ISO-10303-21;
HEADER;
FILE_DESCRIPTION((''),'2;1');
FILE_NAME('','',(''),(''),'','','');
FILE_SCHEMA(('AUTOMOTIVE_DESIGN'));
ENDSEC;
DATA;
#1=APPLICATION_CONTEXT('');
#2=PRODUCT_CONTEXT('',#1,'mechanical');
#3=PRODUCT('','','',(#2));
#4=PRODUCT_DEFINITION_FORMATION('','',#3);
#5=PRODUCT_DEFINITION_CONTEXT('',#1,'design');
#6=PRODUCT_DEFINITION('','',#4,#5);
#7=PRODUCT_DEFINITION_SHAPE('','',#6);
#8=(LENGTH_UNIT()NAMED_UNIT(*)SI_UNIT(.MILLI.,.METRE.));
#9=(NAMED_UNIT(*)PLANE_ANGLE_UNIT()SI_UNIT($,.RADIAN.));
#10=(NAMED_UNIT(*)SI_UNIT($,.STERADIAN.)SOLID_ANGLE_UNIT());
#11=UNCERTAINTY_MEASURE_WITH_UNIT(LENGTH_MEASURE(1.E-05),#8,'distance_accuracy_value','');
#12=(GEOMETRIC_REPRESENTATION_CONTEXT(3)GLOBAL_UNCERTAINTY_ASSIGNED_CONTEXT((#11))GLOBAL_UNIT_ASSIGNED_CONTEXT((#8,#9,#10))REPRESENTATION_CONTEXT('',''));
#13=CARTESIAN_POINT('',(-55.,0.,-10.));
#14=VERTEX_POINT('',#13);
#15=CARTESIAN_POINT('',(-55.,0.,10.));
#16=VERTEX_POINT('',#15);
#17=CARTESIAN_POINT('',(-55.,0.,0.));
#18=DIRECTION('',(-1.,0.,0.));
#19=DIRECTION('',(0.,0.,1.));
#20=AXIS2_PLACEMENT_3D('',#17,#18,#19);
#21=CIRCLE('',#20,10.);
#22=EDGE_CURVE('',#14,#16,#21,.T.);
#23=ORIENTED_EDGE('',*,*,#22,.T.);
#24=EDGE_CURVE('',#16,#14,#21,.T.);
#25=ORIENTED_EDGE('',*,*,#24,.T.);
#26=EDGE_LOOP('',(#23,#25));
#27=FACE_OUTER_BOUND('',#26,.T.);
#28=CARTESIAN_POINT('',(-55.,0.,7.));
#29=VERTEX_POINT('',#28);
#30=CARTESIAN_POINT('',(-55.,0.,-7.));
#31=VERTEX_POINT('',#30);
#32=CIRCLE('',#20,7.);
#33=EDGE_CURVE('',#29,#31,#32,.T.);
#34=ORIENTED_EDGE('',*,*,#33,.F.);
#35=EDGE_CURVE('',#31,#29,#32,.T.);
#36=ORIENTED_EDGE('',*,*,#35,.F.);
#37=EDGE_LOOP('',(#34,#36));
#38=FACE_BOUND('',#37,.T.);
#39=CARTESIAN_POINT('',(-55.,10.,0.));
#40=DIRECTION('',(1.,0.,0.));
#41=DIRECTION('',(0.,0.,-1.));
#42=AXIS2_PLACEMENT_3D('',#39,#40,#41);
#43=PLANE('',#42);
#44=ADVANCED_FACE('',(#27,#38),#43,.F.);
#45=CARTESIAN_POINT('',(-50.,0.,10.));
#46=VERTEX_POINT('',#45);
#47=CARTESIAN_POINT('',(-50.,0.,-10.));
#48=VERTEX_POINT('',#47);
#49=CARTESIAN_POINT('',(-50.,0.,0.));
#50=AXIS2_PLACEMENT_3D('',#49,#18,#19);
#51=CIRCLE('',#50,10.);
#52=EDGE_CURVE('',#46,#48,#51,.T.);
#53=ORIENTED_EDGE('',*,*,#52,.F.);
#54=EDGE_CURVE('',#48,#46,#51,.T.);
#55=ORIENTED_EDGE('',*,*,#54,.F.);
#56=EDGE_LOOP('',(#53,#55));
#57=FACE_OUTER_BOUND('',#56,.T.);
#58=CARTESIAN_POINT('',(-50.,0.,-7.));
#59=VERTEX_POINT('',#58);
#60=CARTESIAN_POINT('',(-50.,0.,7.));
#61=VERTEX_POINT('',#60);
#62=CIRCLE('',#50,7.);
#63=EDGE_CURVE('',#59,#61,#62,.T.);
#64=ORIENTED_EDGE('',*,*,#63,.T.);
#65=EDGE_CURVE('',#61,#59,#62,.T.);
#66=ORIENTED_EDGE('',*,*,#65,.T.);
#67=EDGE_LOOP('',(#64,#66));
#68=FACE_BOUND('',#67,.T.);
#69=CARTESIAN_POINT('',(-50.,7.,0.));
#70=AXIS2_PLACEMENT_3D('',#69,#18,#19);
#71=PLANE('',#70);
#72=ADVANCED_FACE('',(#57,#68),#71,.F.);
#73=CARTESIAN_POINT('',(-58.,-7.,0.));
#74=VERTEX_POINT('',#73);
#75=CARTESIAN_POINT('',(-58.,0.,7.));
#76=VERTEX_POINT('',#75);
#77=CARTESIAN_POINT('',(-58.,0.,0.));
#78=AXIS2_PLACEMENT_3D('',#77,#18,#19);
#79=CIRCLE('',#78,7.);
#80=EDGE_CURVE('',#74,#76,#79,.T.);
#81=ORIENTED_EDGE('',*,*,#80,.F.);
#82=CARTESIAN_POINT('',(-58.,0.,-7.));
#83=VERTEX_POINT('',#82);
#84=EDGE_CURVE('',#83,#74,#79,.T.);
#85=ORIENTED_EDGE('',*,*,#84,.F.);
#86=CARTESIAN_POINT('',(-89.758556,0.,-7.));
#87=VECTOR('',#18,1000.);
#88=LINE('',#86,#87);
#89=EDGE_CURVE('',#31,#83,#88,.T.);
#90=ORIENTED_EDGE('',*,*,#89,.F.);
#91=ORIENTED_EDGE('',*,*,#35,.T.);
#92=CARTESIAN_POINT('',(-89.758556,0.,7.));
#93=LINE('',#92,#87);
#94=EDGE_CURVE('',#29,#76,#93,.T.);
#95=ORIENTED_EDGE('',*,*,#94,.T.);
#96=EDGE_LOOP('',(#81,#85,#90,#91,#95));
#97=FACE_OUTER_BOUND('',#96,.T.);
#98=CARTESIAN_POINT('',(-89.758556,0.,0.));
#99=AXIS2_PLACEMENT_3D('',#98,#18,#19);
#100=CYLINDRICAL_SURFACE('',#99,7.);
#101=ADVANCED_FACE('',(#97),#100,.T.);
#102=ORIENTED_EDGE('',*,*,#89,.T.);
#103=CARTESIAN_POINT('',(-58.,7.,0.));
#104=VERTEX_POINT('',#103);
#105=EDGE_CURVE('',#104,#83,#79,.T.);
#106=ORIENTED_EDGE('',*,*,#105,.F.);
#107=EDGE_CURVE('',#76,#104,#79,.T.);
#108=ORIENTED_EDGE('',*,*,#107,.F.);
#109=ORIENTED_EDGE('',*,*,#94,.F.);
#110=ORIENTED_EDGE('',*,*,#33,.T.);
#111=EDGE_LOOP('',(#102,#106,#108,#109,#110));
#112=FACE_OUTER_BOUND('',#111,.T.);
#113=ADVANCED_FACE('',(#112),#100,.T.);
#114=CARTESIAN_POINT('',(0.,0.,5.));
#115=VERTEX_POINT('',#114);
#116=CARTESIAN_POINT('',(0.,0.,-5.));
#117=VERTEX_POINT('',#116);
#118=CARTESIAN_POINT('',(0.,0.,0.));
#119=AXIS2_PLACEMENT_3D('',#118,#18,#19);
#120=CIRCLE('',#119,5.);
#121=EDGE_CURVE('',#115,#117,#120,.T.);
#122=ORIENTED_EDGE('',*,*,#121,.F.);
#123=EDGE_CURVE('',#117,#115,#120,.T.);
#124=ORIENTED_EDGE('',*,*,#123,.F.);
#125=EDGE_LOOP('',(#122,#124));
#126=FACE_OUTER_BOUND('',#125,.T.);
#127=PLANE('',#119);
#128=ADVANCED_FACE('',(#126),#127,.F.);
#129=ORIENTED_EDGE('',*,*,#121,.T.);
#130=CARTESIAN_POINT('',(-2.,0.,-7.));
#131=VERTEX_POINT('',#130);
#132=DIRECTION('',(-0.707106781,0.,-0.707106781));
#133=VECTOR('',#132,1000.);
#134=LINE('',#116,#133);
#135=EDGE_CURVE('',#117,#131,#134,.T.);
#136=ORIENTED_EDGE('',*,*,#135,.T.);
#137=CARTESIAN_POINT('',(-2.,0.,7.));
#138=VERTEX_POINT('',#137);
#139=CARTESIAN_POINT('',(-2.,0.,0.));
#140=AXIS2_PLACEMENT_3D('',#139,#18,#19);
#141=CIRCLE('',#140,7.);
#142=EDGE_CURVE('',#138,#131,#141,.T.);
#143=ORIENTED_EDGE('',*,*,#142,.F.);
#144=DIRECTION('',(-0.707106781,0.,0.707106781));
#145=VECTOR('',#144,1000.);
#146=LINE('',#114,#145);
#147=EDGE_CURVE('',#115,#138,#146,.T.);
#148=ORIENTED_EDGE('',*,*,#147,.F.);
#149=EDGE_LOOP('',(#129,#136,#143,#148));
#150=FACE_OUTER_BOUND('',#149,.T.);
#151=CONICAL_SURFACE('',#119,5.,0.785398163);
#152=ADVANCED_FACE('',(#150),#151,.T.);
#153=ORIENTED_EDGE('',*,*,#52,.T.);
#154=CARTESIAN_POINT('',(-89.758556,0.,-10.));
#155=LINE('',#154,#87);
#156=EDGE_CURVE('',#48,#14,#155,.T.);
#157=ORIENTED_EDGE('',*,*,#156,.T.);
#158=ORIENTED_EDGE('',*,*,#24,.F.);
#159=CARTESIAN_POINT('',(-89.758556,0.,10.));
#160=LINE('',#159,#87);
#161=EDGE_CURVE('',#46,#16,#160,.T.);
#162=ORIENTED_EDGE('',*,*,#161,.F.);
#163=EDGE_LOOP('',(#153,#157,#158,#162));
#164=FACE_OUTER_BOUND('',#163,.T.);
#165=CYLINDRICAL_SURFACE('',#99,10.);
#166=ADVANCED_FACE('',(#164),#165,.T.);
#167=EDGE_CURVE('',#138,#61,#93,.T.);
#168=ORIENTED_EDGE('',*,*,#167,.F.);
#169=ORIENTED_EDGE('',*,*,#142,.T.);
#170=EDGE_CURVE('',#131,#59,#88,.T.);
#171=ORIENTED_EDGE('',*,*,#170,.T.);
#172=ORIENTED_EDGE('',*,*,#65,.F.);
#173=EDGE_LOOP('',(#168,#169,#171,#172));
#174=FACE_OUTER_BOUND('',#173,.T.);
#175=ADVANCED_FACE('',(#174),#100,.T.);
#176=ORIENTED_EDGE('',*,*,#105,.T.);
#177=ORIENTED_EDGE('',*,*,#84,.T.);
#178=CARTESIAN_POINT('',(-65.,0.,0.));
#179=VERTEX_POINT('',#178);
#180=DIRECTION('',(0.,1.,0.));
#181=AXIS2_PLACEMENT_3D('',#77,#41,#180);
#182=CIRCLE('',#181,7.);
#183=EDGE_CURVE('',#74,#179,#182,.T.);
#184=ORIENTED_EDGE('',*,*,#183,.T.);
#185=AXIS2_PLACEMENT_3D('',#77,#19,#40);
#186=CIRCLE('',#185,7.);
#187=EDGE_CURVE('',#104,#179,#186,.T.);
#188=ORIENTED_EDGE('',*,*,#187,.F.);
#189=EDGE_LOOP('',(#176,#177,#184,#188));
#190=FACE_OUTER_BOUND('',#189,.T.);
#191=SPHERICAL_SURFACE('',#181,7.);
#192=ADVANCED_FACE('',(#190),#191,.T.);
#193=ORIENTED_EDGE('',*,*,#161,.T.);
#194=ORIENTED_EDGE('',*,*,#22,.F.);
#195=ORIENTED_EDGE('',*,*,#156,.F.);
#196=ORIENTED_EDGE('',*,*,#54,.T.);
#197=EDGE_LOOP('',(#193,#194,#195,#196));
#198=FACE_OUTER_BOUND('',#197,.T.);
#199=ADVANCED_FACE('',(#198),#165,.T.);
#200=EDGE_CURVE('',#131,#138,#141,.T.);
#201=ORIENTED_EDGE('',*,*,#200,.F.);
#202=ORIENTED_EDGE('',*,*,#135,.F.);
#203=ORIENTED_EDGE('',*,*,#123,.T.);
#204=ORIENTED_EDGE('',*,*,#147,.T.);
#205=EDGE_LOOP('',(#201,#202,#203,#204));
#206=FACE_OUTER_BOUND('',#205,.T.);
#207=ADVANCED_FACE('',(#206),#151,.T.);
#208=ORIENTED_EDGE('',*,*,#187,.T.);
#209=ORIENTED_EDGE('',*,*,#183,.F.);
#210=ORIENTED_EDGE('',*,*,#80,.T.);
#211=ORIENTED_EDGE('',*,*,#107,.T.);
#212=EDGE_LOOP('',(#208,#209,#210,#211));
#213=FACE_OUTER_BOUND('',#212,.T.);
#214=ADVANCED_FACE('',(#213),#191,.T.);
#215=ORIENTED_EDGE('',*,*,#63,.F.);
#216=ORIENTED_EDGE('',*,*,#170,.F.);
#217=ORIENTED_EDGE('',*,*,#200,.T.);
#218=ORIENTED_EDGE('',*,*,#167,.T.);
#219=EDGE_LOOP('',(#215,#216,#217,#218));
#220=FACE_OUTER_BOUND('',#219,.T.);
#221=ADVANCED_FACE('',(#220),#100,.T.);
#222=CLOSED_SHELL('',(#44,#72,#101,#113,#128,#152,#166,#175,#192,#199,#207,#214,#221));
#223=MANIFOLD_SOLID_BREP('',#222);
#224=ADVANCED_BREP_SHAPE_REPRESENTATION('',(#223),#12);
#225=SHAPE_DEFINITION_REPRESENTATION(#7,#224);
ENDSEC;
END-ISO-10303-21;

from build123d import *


with BuildPart() as part:
    # Sketch1 → Revolve1 (revolve)
    with BuildSketch(Plane.XY, mode=Mode.PRIVATE) as revolve1_sk:
        with BuildLine():
            Line((0, 0), (0, 5))
            Line((0, 5), (-2, 7))
            Line((-2, 7), (-50, 7))
            Line((-50, 7), (-50, 10))
            Line((-50, 10), (-55, 10))
            Line((-55, 10), (-55, 7))
            Line((-55, 7), (-58, 7))
            ThreePointArc((-58, 7), (-62.949747468, 4.949747468), (-65, 0))
            Line((-65, 0), (0, 0))
        make_face()
    revolve(revolve1_sk.sketch.rotate(Axis((-89.758555814, 0, 0), (1, 0, 0)), 90), axis=Axis((-89.758555814, 0, 0), (1, 0, 0)))


solid = part.part
